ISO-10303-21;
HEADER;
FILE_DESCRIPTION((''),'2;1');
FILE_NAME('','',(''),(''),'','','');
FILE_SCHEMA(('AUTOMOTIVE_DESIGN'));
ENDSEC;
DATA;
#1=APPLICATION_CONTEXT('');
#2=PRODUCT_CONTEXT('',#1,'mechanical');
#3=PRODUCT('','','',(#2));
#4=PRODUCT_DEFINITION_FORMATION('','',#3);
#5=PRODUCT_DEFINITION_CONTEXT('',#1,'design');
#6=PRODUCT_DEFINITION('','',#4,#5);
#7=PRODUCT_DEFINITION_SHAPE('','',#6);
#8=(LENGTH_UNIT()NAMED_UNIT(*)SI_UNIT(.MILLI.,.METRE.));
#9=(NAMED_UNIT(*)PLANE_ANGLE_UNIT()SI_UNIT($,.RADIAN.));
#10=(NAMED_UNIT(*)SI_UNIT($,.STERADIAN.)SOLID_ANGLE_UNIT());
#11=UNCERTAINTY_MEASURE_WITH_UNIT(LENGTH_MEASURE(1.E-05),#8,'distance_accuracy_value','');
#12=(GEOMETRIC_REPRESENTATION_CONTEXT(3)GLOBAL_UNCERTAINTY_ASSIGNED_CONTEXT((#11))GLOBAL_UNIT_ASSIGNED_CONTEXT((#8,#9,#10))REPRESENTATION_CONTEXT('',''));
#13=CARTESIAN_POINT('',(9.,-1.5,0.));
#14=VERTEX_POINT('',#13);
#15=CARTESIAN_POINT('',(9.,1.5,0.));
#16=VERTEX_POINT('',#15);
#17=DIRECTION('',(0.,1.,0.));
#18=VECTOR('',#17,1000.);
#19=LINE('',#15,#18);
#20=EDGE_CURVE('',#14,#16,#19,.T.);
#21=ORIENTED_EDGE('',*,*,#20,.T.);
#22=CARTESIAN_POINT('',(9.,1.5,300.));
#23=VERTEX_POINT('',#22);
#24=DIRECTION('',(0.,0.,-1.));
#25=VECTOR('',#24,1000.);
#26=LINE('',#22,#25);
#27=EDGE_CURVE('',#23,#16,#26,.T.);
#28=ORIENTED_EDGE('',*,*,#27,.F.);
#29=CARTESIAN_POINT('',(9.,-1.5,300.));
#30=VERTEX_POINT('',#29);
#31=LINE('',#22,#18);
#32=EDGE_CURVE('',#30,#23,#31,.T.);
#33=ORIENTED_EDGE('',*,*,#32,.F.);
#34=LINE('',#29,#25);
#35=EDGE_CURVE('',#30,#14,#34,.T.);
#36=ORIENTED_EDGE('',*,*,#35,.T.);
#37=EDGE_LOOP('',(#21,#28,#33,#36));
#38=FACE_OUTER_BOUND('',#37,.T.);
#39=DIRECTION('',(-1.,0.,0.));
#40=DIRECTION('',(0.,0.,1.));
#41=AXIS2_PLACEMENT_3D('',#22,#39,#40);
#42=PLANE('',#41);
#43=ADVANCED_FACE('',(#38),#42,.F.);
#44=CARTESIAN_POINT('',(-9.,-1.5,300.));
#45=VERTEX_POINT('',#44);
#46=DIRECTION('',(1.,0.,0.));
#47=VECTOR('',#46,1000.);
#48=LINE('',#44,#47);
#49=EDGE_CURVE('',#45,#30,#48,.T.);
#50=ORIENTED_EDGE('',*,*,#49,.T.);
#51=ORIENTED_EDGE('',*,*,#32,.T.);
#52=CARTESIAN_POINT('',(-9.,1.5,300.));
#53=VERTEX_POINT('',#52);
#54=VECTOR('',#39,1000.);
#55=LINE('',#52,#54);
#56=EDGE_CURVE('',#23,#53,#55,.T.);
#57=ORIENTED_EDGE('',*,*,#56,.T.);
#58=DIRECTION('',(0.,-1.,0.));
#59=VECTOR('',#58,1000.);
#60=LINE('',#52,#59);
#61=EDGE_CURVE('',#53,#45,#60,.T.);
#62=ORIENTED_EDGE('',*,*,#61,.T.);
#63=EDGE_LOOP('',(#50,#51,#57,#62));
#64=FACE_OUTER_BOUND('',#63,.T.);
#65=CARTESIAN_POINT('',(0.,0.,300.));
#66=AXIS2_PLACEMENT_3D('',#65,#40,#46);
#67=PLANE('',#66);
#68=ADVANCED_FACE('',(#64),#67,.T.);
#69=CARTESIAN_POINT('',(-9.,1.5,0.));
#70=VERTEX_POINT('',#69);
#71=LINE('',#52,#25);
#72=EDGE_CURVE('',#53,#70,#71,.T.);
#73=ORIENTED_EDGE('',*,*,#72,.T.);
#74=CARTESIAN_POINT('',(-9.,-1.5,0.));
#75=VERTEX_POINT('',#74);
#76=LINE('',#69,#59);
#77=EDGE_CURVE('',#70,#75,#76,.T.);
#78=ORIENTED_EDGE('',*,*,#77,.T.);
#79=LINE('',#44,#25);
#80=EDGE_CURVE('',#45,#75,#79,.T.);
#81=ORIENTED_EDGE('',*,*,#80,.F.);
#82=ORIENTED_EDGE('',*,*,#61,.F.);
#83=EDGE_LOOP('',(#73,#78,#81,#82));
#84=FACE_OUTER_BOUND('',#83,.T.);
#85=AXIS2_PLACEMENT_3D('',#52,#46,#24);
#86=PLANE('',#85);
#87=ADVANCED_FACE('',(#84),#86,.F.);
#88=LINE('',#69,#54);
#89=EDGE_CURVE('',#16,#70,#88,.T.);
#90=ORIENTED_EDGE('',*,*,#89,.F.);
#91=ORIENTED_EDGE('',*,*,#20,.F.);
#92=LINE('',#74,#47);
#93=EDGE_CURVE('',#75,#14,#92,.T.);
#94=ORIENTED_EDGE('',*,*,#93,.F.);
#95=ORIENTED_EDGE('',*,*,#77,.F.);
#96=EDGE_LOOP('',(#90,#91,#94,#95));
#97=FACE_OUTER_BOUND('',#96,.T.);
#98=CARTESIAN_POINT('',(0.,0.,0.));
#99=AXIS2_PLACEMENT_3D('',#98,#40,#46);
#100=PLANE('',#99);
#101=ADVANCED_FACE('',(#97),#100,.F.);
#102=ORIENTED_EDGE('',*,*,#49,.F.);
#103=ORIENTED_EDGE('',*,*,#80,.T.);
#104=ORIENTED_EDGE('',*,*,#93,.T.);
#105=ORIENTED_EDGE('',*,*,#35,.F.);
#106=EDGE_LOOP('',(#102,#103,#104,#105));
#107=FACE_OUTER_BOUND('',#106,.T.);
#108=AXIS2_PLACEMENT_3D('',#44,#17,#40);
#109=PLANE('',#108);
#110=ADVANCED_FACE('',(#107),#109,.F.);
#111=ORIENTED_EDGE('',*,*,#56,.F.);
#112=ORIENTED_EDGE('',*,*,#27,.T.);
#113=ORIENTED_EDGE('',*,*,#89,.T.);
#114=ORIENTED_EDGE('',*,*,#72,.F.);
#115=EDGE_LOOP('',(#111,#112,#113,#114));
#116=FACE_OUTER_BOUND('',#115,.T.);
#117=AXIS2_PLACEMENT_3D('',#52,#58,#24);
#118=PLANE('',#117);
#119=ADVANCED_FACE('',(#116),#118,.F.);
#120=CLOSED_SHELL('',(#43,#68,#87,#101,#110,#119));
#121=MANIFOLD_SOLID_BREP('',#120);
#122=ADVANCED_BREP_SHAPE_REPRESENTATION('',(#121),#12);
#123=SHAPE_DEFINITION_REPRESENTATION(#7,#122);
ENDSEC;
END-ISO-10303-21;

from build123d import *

# Parameters (mm, degrees)
SKETCH_1_W      = 18
SKETCH_1_H      = 3
EXTRUDE_1_DEPTH = 300


with BuildPart() as part:
    # 草图1 → 凸台-拉伸1 (new body)
    with BuildSketch(Plane.XY):
        Rectangle(SKETCH_1_W, SKETCH_1_H)
    extrude(amount=EXTRUDE_1_DEPTH)


solid = part.part
